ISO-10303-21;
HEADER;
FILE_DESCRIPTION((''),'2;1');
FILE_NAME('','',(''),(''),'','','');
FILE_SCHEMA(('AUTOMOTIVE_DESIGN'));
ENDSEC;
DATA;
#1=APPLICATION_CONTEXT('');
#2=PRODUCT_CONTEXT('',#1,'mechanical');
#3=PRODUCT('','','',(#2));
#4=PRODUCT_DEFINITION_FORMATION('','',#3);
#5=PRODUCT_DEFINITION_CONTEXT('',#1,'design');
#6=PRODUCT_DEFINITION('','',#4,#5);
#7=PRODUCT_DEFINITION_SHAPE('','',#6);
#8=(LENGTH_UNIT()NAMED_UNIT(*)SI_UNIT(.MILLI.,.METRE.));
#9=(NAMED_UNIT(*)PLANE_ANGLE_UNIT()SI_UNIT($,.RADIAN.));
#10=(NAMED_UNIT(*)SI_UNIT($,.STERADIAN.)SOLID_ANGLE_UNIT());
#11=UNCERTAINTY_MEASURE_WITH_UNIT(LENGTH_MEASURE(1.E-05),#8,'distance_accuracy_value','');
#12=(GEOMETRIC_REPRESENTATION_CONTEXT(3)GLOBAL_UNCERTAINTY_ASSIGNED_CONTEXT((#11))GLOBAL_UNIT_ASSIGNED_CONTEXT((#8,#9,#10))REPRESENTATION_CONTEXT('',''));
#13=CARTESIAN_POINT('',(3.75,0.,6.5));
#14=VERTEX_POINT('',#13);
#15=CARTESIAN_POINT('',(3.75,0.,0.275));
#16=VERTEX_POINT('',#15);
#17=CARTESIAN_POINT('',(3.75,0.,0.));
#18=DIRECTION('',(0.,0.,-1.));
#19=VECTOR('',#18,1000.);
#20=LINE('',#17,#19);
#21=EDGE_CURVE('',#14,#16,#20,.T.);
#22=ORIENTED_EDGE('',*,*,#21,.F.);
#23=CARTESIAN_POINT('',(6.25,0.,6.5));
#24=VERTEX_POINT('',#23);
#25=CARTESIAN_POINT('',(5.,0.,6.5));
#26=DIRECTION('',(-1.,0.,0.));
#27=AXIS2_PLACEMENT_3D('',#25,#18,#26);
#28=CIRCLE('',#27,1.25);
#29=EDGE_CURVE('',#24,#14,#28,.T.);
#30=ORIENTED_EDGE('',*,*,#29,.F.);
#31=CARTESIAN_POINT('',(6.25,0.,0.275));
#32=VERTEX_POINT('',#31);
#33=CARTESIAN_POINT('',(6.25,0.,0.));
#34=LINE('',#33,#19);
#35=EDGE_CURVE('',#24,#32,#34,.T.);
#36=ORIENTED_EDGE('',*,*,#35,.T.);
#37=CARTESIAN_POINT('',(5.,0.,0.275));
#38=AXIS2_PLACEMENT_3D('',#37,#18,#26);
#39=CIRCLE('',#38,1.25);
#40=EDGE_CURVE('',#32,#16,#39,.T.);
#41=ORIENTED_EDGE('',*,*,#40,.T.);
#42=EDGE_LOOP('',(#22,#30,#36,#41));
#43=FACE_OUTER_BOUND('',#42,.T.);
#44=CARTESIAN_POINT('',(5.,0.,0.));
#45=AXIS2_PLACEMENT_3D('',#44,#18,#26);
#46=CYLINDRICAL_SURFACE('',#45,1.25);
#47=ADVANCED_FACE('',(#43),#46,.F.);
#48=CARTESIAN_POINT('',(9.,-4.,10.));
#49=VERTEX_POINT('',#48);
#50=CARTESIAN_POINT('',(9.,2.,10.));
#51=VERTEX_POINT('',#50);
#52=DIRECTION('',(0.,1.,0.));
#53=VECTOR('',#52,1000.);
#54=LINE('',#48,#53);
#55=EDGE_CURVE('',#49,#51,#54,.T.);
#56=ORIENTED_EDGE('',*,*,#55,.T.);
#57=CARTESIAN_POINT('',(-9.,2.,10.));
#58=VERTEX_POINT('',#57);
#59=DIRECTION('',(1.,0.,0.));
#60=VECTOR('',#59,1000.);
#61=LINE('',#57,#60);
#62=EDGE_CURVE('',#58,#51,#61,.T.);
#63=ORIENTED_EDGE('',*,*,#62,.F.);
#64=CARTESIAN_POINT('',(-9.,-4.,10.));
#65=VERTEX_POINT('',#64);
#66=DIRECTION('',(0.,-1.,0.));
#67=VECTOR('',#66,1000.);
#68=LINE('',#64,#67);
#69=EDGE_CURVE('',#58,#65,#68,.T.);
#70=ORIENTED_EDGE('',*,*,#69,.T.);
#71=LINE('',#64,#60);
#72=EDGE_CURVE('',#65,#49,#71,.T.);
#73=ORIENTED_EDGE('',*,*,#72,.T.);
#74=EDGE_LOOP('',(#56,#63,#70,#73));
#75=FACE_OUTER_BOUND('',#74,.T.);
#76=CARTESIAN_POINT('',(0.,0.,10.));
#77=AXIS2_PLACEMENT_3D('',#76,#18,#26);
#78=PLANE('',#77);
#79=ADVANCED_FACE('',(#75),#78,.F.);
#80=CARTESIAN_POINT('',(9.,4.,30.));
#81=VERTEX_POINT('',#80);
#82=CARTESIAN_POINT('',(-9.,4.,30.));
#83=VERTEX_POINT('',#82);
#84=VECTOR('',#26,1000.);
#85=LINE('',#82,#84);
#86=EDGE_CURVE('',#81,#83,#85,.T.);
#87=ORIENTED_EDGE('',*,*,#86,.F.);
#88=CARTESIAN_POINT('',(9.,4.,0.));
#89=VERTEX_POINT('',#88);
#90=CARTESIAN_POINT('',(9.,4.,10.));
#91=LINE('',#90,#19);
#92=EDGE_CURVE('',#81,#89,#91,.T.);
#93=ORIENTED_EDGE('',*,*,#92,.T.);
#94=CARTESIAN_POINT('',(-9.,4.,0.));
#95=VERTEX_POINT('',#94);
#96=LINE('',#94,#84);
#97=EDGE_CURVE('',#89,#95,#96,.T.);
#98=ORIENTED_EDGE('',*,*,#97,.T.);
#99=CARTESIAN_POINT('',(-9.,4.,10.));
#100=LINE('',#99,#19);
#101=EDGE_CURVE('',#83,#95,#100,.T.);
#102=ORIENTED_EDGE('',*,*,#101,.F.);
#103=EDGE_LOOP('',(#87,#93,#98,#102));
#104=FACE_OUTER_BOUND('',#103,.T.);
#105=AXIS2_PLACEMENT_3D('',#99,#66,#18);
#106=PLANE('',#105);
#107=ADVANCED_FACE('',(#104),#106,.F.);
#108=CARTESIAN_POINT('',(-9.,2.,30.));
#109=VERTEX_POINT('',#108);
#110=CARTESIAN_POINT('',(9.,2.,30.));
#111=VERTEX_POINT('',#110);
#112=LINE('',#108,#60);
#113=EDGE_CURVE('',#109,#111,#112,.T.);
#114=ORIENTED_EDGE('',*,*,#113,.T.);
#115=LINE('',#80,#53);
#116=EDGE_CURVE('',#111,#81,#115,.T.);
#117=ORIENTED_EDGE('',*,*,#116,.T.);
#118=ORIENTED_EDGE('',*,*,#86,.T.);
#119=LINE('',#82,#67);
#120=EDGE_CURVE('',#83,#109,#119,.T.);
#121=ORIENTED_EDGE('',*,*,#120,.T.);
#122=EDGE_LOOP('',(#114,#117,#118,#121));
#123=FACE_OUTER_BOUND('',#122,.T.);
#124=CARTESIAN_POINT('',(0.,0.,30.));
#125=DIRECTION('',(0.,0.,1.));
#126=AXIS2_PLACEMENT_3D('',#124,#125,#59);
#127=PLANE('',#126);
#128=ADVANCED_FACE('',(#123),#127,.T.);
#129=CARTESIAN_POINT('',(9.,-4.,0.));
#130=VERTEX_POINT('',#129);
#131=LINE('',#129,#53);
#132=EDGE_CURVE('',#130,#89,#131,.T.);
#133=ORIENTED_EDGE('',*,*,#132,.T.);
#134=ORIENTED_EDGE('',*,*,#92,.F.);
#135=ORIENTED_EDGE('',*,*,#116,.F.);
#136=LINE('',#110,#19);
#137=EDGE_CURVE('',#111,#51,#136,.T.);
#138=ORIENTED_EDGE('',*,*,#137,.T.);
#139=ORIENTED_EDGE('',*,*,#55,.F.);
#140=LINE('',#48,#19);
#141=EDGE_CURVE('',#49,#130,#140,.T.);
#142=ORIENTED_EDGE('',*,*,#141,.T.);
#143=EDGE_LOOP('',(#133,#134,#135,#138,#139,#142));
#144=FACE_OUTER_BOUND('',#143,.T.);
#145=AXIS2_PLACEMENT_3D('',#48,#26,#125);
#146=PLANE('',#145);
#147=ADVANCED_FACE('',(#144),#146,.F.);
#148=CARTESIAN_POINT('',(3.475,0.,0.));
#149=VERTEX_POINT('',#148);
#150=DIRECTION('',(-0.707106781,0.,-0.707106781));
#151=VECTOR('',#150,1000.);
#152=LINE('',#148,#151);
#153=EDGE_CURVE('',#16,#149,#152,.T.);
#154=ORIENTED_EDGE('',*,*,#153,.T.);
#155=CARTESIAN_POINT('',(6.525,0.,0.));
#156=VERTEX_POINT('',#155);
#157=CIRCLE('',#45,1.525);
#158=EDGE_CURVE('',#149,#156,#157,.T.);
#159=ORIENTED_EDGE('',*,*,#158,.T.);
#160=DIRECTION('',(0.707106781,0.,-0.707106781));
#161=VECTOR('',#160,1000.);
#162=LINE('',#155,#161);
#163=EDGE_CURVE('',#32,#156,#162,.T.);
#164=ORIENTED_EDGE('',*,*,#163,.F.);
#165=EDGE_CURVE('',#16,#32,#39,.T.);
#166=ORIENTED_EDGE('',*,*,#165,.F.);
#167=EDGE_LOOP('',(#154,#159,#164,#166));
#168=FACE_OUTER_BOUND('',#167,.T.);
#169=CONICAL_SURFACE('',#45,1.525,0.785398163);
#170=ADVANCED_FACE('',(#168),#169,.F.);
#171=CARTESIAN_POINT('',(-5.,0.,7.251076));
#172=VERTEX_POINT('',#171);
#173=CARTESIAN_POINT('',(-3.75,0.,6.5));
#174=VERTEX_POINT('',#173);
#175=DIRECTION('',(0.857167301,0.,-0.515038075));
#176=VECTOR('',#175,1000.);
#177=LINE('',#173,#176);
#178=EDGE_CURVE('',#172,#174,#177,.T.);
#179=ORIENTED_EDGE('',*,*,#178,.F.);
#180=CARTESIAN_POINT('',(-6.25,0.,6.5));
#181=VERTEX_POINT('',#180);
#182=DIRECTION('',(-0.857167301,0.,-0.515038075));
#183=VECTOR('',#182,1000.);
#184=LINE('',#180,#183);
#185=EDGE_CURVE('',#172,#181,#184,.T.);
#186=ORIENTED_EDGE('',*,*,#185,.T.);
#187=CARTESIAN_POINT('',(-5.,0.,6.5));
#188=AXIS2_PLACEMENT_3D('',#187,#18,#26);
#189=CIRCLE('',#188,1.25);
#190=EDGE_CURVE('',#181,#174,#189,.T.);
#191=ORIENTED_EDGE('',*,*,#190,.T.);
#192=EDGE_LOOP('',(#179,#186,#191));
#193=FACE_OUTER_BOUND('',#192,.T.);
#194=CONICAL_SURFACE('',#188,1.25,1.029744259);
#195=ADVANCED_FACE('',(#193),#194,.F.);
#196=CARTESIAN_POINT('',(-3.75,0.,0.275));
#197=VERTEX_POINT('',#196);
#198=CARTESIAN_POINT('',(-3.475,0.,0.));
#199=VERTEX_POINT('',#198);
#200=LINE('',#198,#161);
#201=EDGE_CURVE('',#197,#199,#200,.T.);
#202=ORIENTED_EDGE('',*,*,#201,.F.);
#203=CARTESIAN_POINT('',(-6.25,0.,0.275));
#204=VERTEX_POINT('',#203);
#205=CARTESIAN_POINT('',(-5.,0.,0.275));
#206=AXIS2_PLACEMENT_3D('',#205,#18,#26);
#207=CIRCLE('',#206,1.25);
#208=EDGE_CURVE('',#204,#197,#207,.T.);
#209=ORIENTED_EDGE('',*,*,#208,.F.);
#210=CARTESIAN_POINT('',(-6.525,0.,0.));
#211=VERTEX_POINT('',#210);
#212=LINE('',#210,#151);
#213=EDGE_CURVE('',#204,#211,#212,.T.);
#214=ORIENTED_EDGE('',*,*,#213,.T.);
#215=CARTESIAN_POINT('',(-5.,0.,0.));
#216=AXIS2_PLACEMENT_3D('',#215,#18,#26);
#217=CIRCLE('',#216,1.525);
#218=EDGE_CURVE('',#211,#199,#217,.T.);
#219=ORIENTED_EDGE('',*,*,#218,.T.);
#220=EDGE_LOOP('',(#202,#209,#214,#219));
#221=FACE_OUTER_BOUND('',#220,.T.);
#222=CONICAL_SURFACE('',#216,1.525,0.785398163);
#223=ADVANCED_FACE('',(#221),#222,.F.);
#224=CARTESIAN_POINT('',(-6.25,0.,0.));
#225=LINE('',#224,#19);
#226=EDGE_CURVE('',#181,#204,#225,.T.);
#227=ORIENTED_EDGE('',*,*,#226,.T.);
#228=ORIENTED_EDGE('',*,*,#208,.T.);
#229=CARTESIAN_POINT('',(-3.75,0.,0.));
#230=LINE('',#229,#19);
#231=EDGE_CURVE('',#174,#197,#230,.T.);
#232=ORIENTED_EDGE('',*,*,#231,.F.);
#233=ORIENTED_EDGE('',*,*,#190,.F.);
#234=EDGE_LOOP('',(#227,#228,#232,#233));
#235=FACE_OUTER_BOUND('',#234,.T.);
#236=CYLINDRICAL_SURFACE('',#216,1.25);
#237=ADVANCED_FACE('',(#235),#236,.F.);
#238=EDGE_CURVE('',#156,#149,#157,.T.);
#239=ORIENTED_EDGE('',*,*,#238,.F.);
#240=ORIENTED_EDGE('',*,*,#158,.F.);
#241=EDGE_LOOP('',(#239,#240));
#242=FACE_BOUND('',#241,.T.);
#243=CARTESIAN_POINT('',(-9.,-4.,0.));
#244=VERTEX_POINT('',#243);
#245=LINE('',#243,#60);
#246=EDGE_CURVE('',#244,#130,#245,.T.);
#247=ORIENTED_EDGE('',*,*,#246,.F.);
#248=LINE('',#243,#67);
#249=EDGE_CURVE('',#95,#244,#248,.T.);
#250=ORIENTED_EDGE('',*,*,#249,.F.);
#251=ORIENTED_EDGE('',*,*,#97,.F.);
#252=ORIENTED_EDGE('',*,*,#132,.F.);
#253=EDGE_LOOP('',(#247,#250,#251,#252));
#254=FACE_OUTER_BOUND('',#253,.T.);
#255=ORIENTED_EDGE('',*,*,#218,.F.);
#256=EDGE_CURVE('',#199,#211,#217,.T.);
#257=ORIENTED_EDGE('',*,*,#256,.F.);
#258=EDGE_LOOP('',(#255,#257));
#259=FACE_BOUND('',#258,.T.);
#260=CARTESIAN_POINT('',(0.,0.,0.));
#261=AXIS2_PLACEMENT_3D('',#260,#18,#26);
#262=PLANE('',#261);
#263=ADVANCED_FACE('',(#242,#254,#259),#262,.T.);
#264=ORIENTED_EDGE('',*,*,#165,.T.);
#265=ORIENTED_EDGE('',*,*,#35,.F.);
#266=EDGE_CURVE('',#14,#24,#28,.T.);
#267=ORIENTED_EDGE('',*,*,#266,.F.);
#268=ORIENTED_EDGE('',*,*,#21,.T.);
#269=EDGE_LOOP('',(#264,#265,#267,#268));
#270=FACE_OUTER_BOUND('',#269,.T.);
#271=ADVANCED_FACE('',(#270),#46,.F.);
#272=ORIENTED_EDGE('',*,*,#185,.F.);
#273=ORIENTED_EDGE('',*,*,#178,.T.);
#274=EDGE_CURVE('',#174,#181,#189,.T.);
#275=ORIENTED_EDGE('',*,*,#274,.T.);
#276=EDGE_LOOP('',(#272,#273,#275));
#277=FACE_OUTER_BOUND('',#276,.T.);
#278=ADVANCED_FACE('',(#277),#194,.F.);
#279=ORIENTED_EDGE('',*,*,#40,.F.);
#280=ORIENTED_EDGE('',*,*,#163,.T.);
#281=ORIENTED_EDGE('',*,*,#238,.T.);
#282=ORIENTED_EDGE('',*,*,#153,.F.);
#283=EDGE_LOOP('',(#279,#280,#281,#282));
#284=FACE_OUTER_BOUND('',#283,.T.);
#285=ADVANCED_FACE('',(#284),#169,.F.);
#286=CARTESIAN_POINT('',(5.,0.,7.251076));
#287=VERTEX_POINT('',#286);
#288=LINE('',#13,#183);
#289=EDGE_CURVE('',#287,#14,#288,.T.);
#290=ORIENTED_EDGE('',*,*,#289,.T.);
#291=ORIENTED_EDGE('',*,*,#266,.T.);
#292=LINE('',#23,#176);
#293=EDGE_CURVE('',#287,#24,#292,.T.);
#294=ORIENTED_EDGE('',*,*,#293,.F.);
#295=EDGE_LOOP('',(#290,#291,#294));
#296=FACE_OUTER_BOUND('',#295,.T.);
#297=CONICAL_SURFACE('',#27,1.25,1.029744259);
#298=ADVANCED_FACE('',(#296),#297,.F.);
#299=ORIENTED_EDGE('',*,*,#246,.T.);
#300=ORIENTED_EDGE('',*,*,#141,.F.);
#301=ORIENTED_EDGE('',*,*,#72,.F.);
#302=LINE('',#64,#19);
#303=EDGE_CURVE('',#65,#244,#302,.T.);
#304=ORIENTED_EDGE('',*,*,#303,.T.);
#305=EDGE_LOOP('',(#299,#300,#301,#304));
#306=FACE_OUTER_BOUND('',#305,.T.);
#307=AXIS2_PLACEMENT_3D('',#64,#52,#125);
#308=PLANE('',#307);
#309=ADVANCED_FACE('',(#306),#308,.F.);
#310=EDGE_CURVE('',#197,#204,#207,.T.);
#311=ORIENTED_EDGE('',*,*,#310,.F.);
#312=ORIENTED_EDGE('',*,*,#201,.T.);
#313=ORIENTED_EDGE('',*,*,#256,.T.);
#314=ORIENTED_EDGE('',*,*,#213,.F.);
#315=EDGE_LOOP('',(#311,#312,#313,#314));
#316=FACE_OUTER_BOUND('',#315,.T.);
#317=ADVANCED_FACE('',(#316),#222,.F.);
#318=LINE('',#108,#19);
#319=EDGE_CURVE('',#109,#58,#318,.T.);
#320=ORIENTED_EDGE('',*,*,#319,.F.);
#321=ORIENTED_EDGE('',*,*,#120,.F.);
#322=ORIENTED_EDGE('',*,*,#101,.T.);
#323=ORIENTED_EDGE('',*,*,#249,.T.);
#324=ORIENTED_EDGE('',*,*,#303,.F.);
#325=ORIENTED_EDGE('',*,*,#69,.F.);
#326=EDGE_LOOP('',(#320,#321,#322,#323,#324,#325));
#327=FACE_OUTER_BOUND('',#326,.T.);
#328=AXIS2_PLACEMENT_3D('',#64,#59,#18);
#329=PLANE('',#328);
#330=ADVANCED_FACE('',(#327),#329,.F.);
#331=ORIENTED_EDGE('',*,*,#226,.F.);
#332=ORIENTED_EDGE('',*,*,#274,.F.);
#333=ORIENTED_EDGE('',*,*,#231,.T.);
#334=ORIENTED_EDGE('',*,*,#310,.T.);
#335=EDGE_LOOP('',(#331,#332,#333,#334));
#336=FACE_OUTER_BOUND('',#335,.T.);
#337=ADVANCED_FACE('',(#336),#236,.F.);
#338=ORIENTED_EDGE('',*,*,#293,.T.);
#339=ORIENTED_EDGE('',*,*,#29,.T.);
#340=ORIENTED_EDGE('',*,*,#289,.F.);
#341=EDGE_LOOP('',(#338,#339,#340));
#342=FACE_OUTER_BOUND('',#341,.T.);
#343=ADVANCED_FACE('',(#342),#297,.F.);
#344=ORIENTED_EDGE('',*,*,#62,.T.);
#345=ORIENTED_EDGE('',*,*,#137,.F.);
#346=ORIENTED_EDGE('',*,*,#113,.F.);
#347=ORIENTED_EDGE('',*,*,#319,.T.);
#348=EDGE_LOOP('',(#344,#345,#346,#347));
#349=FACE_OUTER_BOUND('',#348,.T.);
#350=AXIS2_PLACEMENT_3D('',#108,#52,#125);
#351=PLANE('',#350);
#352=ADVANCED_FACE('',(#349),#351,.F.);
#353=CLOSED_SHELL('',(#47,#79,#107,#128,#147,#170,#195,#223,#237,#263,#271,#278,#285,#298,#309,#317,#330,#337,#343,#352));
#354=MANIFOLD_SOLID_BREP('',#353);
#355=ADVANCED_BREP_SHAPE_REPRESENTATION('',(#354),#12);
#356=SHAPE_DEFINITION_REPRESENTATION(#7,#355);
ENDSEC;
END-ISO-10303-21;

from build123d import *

# Parameters (mm, degrees)
SKETCH_1_W      = 18
SKETCH_1_H      = 8
EXTRUDE_1_DEPTH = 10
SKETCH_2_W      = 18
SKETCH_2_H      = 2
EXTRUDE_2_DEPTH = 20


with BuildPart() as part:
    # 草图1 → 凸台-拉伸1 (new body)
    with BuildSketch(Plane.XY):
        Rectangle(SKETCH_1_W, SKETCH_1_H)
    extrude(amount=EXTRUDE_1_DEPTH)

    # 草图2 → 凸台-拉伸2 (add)
    with BuildSketch(Plane.XY.offset(10)):
        with Locations((0, 3)):
            Rectangle(SKETCH_2_W, SKETCH_2_H)
    extrude(amount=EXTRUDE_2_DEPTH)

    # 草图3 → M3 螺纹孔1 (revolve, cut)
    with BuildSketch(Plane.YZ.offset(5)):
        Polygon((0, 0), (0, 7.251075774), (1.25, 6.5), (1.25, 0.275), (1.525, 0), align=None)
    hole_wizard_m3_1 = revolve(axis=Axis((5, 0, -6.35), (0, 0, 1)), mode=Mode.SUBTRACT)

    # 镜向1: M3 螺纹孔1 across plane
    add(hole_wizard_m3_1.mirror(Plane(origin=(0, 0, 0), x_dir=(0, 0, 1), z_dir=(1, 0, 0))), mode=Mode.SUBTRACT)


solid = part.part
